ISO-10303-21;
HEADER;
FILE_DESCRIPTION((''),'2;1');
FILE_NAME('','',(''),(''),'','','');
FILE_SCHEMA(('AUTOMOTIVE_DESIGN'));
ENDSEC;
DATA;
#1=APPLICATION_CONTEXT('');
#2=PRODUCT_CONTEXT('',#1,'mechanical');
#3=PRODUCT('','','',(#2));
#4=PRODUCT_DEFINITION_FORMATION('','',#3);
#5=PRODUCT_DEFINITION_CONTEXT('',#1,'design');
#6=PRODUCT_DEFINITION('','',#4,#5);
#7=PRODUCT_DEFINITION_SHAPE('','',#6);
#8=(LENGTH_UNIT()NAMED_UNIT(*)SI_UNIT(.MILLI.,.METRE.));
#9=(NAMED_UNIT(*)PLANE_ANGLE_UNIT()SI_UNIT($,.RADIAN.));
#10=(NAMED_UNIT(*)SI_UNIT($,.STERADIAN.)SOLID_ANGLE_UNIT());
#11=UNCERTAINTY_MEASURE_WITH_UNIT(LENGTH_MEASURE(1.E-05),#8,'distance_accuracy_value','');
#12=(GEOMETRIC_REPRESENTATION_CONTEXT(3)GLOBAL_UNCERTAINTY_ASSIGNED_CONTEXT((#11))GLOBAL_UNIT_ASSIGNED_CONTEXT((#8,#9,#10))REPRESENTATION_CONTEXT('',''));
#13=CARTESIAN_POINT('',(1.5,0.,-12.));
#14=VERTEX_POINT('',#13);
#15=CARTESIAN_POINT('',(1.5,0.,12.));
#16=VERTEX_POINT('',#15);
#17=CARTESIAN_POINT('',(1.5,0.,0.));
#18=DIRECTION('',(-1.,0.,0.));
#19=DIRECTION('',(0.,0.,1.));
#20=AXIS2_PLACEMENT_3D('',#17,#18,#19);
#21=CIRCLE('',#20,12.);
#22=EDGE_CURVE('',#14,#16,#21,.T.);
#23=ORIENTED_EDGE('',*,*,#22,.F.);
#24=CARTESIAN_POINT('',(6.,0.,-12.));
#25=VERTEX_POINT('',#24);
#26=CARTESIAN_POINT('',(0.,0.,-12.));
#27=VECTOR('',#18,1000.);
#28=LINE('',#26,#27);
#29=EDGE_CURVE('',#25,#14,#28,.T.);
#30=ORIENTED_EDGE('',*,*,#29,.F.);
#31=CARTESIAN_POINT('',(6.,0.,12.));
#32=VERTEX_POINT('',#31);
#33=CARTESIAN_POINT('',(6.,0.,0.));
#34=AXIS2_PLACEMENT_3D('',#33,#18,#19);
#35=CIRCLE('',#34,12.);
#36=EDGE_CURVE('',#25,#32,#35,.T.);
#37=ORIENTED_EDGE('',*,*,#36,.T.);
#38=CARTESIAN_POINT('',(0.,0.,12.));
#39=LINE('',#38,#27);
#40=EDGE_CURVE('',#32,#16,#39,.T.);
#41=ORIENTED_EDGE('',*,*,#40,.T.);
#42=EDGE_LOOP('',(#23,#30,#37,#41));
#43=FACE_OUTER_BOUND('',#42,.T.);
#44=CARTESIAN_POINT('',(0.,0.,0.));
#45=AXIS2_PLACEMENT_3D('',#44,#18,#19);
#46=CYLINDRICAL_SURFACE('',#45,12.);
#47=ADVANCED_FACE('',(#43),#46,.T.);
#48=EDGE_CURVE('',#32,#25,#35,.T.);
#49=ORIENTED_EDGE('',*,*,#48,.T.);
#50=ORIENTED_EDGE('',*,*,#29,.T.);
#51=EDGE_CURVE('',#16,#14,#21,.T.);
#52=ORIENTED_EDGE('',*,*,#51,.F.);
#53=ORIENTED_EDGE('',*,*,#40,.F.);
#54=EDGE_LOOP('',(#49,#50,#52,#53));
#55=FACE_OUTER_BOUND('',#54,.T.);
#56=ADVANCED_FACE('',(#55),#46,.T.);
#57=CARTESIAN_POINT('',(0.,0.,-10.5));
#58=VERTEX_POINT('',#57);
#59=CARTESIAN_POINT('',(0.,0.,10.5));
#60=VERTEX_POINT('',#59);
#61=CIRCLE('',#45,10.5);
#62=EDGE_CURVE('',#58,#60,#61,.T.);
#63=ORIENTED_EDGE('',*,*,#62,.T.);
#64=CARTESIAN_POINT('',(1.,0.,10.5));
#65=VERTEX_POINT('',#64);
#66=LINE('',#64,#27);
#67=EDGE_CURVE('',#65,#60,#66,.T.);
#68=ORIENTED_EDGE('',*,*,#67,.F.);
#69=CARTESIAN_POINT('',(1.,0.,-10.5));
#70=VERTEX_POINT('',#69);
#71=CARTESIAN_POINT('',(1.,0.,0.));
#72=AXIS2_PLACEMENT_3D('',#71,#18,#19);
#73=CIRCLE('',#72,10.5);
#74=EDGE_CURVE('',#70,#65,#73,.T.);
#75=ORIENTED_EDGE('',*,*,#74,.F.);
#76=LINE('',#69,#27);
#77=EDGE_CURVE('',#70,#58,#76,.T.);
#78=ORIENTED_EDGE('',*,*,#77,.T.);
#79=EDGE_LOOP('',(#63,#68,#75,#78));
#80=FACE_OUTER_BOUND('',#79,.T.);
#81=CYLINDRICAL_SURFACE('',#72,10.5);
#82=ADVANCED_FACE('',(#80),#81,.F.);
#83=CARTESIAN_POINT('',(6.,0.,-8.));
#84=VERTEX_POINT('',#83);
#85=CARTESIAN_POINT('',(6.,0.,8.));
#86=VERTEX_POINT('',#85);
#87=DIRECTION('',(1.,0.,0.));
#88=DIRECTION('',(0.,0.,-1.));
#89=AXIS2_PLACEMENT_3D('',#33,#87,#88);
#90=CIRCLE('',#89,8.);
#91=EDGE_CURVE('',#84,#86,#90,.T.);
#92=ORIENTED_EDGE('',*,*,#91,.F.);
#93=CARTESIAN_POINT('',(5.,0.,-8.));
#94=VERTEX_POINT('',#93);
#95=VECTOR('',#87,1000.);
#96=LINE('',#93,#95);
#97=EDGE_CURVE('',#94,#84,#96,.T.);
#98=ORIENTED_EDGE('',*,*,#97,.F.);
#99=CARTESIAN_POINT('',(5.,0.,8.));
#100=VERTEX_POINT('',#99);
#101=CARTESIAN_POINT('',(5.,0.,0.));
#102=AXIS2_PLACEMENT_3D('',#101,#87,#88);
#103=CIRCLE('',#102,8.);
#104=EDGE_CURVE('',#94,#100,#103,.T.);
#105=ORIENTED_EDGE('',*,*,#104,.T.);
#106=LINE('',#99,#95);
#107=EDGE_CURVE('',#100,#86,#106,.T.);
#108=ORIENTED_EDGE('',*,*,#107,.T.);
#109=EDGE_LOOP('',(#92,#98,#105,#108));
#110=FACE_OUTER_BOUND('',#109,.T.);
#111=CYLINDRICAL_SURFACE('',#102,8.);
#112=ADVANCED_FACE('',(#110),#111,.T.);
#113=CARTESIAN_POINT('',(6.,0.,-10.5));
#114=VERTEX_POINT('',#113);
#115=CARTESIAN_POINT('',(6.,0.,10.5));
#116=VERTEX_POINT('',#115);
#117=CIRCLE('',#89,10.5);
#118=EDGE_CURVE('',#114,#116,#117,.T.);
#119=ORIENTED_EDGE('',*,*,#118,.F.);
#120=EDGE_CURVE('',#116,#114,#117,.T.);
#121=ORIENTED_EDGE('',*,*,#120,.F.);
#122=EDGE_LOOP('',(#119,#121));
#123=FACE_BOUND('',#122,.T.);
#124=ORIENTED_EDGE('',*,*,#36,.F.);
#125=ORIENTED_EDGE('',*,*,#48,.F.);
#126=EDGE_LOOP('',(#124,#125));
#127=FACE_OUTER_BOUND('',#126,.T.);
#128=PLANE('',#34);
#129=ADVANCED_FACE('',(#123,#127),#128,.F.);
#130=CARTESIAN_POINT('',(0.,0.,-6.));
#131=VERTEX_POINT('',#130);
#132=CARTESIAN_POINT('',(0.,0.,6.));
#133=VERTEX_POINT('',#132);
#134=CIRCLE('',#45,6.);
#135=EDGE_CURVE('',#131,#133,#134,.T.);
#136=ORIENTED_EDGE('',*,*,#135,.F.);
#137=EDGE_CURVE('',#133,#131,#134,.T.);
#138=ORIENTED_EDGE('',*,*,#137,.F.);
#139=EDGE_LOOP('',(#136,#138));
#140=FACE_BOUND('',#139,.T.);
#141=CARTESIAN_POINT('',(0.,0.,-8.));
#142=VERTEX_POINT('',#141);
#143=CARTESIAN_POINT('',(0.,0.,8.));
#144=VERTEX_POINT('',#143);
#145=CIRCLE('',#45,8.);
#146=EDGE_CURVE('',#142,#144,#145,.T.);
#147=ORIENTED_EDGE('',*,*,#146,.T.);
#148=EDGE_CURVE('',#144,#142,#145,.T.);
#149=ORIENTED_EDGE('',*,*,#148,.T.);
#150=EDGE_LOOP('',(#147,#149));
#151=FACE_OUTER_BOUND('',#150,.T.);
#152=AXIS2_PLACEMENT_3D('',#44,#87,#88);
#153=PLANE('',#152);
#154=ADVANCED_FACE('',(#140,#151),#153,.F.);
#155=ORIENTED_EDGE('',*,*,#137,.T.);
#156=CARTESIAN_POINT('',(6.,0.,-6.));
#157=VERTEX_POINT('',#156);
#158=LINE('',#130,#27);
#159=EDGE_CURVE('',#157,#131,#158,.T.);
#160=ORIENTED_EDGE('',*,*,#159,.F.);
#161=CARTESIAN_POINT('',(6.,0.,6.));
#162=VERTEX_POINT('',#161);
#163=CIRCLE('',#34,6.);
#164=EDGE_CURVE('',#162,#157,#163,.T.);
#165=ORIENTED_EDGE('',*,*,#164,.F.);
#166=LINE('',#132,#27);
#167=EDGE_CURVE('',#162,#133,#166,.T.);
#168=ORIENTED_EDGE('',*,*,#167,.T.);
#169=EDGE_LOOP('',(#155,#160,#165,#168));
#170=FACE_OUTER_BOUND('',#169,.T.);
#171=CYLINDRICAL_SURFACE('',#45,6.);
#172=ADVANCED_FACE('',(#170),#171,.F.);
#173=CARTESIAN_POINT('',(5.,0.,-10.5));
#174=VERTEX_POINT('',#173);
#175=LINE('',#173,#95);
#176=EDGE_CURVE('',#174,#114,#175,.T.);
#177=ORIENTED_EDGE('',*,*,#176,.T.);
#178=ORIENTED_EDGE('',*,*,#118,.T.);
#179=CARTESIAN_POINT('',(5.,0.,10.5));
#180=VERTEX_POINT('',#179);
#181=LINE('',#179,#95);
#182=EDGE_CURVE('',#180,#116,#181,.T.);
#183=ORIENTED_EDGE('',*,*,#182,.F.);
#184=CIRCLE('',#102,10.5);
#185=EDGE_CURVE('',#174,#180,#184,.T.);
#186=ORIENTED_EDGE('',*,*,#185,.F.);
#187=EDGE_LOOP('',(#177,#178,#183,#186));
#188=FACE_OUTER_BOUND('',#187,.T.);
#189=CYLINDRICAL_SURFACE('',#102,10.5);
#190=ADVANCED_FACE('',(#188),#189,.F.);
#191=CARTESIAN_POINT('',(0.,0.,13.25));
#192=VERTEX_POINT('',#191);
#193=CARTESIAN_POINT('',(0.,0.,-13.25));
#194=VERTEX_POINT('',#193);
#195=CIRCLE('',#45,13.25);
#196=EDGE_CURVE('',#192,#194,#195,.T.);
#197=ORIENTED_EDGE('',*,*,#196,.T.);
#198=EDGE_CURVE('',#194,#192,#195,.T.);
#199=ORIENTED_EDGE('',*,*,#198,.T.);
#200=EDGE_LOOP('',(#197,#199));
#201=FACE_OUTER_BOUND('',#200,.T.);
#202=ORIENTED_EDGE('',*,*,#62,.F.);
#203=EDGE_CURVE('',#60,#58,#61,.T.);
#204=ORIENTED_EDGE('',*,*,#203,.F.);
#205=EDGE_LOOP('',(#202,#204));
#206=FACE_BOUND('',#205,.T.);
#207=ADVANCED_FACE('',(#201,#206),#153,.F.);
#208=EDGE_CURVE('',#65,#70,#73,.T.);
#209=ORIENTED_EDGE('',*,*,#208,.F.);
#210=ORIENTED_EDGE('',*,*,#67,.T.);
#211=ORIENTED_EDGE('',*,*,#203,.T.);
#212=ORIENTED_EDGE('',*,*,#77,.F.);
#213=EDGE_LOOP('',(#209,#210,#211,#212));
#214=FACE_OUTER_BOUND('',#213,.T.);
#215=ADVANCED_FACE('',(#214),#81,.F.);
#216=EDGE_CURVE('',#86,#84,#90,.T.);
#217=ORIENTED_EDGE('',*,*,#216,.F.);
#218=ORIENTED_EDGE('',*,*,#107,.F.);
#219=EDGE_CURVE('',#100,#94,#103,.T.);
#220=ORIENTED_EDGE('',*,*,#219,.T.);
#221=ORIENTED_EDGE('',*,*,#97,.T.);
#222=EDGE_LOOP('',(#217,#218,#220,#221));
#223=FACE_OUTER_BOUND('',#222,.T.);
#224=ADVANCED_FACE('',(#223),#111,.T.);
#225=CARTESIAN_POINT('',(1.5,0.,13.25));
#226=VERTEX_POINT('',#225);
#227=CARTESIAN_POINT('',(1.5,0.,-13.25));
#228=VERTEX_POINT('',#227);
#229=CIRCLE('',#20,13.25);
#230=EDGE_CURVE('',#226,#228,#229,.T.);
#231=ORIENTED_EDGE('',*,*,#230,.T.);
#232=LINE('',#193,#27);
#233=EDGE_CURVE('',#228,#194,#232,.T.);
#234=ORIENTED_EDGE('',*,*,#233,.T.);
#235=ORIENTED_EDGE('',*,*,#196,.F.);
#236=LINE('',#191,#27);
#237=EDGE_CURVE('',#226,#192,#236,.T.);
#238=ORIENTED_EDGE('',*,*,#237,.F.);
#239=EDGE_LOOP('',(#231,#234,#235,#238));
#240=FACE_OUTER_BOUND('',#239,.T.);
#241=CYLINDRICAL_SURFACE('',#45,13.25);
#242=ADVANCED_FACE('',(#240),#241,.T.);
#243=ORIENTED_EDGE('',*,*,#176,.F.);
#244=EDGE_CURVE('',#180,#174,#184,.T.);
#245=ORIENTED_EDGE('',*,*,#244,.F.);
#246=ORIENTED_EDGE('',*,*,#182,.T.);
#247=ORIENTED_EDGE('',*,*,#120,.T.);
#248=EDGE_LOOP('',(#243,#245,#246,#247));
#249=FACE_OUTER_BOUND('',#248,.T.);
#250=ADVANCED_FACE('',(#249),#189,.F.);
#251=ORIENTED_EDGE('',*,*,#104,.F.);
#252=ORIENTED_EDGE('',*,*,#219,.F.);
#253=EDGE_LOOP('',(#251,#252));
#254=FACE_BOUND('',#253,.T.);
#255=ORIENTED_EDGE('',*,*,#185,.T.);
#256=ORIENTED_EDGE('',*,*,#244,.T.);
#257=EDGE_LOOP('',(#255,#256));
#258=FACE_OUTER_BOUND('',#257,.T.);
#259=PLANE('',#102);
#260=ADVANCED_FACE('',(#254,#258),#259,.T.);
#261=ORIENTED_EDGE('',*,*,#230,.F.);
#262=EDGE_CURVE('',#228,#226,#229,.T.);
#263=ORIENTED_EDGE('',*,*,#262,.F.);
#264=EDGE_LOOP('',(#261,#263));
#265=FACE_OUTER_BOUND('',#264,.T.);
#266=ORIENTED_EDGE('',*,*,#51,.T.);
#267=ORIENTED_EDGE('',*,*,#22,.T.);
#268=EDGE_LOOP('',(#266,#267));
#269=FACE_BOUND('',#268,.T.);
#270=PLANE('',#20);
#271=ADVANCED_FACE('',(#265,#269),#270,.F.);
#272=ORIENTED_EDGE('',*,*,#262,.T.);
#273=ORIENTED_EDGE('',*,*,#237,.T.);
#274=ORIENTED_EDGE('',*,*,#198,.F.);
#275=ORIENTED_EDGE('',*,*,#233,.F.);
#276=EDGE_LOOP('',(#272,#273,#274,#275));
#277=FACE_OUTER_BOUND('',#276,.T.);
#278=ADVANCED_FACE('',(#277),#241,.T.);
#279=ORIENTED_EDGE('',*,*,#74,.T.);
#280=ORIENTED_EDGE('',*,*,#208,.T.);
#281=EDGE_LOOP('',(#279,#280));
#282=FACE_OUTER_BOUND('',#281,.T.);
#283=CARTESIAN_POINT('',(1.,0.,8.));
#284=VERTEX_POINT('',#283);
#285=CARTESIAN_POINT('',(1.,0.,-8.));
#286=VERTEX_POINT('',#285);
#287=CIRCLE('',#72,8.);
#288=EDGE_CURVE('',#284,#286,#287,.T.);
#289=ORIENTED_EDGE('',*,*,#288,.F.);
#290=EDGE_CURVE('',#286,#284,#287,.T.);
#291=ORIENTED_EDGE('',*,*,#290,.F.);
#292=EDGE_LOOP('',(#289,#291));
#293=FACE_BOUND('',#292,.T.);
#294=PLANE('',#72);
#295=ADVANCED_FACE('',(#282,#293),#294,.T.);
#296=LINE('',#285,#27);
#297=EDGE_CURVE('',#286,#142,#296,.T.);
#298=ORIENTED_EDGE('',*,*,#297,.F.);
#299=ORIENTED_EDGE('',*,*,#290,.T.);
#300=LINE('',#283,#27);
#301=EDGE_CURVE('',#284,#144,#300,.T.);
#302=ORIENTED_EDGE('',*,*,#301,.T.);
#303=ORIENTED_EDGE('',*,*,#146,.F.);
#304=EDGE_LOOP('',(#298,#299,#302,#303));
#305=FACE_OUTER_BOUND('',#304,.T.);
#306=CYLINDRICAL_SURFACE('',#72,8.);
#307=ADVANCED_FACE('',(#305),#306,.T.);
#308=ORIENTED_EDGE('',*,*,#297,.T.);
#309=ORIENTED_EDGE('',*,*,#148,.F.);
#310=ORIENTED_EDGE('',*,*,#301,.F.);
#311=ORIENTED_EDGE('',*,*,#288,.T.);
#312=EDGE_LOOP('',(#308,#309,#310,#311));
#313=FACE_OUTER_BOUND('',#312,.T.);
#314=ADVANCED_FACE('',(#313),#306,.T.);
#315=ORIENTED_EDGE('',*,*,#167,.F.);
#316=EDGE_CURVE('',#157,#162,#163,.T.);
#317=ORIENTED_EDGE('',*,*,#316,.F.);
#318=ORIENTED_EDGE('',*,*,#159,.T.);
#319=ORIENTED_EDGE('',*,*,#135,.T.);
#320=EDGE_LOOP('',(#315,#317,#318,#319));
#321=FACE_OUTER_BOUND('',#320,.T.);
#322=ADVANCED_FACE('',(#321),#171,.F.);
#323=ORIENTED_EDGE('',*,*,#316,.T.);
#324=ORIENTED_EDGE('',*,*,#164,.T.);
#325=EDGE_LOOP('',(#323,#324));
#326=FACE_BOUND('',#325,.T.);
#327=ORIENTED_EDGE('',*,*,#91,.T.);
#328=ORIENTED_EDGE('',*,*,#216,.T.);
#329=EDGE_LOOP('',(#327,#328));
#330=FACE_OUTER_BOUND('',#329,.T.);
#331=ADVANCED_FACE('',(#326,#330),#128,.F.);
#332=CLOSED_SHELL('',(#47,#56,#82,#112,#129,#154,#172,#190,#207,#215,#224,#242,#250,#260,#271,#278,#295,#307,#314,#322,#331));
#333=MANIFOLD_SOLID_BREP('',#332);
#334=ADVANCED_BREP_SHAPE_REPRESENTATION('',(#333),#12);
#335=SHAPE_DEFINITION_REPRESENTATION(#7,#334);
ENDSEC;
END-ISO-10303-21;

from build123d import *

# Parameters (mm, degrees)
SKETCH2_R          = 10.5
SKETCH2_R_2        = 8
CUT_EXTRUDE1_DEPTH = 1
CUT_EXTRUDE2_START = -1
SKETCH3_R          = 10.5
SKETCH3_R_2        = 8
CUT_EXTRUDE2_DEPTH = 1


with BuildPart() as part:
    # Sketch1 → Revolve1 (revolve)
    with BuildSketch(Plane.XY, mode=Mode.PRIVATE) as revolve1_sk:
        Polygon((0, 6), (6, 6), (6, 12), (1.5, 12), (1.5, 13.25), (0, 13.25), align=None)
    revolve(revolve1_sk.sketch.rotate(Axis((0, 0, 0), (1, 0, 0)), 90), axis=Axis((0, 0, 0), (1, 0, 0)))

    # Sketch2 → Cut-Extrude1 (cut)
    with BuildSketch(Plane(origin=(6, 0, 0), x_dir=(0, 0, -1), z_dir=(1, 0, 0))):
        Circle(SKETCH2_R)
        Circle(SKETCH2_R_2, mode=Mode.SUBTRACT)
    extrude(amount=-CUT_EXTRUDE1_DEPTH, mode=Mode.SUBTRACT)

    # Sketch3 → Cut-Extrude2 (cut)
    with BuildSketch(Plane.ZY.offset(CUT_EXTRUDE2_START)):
        with Locations(Location((0, 0, 0), (0, 0, 180))):
            Circle(SKETCH3_R)
        with Locations(Location((0, 0, 0), (0, 0, 180))):
            Circle(SKETCH3_R_2, mode=Mode.SUBTRACT)
    extrude(amount=CUT_EXTRUDE2_DEPTH, mode=Mode.SUBTRACT)


solid = part.part
